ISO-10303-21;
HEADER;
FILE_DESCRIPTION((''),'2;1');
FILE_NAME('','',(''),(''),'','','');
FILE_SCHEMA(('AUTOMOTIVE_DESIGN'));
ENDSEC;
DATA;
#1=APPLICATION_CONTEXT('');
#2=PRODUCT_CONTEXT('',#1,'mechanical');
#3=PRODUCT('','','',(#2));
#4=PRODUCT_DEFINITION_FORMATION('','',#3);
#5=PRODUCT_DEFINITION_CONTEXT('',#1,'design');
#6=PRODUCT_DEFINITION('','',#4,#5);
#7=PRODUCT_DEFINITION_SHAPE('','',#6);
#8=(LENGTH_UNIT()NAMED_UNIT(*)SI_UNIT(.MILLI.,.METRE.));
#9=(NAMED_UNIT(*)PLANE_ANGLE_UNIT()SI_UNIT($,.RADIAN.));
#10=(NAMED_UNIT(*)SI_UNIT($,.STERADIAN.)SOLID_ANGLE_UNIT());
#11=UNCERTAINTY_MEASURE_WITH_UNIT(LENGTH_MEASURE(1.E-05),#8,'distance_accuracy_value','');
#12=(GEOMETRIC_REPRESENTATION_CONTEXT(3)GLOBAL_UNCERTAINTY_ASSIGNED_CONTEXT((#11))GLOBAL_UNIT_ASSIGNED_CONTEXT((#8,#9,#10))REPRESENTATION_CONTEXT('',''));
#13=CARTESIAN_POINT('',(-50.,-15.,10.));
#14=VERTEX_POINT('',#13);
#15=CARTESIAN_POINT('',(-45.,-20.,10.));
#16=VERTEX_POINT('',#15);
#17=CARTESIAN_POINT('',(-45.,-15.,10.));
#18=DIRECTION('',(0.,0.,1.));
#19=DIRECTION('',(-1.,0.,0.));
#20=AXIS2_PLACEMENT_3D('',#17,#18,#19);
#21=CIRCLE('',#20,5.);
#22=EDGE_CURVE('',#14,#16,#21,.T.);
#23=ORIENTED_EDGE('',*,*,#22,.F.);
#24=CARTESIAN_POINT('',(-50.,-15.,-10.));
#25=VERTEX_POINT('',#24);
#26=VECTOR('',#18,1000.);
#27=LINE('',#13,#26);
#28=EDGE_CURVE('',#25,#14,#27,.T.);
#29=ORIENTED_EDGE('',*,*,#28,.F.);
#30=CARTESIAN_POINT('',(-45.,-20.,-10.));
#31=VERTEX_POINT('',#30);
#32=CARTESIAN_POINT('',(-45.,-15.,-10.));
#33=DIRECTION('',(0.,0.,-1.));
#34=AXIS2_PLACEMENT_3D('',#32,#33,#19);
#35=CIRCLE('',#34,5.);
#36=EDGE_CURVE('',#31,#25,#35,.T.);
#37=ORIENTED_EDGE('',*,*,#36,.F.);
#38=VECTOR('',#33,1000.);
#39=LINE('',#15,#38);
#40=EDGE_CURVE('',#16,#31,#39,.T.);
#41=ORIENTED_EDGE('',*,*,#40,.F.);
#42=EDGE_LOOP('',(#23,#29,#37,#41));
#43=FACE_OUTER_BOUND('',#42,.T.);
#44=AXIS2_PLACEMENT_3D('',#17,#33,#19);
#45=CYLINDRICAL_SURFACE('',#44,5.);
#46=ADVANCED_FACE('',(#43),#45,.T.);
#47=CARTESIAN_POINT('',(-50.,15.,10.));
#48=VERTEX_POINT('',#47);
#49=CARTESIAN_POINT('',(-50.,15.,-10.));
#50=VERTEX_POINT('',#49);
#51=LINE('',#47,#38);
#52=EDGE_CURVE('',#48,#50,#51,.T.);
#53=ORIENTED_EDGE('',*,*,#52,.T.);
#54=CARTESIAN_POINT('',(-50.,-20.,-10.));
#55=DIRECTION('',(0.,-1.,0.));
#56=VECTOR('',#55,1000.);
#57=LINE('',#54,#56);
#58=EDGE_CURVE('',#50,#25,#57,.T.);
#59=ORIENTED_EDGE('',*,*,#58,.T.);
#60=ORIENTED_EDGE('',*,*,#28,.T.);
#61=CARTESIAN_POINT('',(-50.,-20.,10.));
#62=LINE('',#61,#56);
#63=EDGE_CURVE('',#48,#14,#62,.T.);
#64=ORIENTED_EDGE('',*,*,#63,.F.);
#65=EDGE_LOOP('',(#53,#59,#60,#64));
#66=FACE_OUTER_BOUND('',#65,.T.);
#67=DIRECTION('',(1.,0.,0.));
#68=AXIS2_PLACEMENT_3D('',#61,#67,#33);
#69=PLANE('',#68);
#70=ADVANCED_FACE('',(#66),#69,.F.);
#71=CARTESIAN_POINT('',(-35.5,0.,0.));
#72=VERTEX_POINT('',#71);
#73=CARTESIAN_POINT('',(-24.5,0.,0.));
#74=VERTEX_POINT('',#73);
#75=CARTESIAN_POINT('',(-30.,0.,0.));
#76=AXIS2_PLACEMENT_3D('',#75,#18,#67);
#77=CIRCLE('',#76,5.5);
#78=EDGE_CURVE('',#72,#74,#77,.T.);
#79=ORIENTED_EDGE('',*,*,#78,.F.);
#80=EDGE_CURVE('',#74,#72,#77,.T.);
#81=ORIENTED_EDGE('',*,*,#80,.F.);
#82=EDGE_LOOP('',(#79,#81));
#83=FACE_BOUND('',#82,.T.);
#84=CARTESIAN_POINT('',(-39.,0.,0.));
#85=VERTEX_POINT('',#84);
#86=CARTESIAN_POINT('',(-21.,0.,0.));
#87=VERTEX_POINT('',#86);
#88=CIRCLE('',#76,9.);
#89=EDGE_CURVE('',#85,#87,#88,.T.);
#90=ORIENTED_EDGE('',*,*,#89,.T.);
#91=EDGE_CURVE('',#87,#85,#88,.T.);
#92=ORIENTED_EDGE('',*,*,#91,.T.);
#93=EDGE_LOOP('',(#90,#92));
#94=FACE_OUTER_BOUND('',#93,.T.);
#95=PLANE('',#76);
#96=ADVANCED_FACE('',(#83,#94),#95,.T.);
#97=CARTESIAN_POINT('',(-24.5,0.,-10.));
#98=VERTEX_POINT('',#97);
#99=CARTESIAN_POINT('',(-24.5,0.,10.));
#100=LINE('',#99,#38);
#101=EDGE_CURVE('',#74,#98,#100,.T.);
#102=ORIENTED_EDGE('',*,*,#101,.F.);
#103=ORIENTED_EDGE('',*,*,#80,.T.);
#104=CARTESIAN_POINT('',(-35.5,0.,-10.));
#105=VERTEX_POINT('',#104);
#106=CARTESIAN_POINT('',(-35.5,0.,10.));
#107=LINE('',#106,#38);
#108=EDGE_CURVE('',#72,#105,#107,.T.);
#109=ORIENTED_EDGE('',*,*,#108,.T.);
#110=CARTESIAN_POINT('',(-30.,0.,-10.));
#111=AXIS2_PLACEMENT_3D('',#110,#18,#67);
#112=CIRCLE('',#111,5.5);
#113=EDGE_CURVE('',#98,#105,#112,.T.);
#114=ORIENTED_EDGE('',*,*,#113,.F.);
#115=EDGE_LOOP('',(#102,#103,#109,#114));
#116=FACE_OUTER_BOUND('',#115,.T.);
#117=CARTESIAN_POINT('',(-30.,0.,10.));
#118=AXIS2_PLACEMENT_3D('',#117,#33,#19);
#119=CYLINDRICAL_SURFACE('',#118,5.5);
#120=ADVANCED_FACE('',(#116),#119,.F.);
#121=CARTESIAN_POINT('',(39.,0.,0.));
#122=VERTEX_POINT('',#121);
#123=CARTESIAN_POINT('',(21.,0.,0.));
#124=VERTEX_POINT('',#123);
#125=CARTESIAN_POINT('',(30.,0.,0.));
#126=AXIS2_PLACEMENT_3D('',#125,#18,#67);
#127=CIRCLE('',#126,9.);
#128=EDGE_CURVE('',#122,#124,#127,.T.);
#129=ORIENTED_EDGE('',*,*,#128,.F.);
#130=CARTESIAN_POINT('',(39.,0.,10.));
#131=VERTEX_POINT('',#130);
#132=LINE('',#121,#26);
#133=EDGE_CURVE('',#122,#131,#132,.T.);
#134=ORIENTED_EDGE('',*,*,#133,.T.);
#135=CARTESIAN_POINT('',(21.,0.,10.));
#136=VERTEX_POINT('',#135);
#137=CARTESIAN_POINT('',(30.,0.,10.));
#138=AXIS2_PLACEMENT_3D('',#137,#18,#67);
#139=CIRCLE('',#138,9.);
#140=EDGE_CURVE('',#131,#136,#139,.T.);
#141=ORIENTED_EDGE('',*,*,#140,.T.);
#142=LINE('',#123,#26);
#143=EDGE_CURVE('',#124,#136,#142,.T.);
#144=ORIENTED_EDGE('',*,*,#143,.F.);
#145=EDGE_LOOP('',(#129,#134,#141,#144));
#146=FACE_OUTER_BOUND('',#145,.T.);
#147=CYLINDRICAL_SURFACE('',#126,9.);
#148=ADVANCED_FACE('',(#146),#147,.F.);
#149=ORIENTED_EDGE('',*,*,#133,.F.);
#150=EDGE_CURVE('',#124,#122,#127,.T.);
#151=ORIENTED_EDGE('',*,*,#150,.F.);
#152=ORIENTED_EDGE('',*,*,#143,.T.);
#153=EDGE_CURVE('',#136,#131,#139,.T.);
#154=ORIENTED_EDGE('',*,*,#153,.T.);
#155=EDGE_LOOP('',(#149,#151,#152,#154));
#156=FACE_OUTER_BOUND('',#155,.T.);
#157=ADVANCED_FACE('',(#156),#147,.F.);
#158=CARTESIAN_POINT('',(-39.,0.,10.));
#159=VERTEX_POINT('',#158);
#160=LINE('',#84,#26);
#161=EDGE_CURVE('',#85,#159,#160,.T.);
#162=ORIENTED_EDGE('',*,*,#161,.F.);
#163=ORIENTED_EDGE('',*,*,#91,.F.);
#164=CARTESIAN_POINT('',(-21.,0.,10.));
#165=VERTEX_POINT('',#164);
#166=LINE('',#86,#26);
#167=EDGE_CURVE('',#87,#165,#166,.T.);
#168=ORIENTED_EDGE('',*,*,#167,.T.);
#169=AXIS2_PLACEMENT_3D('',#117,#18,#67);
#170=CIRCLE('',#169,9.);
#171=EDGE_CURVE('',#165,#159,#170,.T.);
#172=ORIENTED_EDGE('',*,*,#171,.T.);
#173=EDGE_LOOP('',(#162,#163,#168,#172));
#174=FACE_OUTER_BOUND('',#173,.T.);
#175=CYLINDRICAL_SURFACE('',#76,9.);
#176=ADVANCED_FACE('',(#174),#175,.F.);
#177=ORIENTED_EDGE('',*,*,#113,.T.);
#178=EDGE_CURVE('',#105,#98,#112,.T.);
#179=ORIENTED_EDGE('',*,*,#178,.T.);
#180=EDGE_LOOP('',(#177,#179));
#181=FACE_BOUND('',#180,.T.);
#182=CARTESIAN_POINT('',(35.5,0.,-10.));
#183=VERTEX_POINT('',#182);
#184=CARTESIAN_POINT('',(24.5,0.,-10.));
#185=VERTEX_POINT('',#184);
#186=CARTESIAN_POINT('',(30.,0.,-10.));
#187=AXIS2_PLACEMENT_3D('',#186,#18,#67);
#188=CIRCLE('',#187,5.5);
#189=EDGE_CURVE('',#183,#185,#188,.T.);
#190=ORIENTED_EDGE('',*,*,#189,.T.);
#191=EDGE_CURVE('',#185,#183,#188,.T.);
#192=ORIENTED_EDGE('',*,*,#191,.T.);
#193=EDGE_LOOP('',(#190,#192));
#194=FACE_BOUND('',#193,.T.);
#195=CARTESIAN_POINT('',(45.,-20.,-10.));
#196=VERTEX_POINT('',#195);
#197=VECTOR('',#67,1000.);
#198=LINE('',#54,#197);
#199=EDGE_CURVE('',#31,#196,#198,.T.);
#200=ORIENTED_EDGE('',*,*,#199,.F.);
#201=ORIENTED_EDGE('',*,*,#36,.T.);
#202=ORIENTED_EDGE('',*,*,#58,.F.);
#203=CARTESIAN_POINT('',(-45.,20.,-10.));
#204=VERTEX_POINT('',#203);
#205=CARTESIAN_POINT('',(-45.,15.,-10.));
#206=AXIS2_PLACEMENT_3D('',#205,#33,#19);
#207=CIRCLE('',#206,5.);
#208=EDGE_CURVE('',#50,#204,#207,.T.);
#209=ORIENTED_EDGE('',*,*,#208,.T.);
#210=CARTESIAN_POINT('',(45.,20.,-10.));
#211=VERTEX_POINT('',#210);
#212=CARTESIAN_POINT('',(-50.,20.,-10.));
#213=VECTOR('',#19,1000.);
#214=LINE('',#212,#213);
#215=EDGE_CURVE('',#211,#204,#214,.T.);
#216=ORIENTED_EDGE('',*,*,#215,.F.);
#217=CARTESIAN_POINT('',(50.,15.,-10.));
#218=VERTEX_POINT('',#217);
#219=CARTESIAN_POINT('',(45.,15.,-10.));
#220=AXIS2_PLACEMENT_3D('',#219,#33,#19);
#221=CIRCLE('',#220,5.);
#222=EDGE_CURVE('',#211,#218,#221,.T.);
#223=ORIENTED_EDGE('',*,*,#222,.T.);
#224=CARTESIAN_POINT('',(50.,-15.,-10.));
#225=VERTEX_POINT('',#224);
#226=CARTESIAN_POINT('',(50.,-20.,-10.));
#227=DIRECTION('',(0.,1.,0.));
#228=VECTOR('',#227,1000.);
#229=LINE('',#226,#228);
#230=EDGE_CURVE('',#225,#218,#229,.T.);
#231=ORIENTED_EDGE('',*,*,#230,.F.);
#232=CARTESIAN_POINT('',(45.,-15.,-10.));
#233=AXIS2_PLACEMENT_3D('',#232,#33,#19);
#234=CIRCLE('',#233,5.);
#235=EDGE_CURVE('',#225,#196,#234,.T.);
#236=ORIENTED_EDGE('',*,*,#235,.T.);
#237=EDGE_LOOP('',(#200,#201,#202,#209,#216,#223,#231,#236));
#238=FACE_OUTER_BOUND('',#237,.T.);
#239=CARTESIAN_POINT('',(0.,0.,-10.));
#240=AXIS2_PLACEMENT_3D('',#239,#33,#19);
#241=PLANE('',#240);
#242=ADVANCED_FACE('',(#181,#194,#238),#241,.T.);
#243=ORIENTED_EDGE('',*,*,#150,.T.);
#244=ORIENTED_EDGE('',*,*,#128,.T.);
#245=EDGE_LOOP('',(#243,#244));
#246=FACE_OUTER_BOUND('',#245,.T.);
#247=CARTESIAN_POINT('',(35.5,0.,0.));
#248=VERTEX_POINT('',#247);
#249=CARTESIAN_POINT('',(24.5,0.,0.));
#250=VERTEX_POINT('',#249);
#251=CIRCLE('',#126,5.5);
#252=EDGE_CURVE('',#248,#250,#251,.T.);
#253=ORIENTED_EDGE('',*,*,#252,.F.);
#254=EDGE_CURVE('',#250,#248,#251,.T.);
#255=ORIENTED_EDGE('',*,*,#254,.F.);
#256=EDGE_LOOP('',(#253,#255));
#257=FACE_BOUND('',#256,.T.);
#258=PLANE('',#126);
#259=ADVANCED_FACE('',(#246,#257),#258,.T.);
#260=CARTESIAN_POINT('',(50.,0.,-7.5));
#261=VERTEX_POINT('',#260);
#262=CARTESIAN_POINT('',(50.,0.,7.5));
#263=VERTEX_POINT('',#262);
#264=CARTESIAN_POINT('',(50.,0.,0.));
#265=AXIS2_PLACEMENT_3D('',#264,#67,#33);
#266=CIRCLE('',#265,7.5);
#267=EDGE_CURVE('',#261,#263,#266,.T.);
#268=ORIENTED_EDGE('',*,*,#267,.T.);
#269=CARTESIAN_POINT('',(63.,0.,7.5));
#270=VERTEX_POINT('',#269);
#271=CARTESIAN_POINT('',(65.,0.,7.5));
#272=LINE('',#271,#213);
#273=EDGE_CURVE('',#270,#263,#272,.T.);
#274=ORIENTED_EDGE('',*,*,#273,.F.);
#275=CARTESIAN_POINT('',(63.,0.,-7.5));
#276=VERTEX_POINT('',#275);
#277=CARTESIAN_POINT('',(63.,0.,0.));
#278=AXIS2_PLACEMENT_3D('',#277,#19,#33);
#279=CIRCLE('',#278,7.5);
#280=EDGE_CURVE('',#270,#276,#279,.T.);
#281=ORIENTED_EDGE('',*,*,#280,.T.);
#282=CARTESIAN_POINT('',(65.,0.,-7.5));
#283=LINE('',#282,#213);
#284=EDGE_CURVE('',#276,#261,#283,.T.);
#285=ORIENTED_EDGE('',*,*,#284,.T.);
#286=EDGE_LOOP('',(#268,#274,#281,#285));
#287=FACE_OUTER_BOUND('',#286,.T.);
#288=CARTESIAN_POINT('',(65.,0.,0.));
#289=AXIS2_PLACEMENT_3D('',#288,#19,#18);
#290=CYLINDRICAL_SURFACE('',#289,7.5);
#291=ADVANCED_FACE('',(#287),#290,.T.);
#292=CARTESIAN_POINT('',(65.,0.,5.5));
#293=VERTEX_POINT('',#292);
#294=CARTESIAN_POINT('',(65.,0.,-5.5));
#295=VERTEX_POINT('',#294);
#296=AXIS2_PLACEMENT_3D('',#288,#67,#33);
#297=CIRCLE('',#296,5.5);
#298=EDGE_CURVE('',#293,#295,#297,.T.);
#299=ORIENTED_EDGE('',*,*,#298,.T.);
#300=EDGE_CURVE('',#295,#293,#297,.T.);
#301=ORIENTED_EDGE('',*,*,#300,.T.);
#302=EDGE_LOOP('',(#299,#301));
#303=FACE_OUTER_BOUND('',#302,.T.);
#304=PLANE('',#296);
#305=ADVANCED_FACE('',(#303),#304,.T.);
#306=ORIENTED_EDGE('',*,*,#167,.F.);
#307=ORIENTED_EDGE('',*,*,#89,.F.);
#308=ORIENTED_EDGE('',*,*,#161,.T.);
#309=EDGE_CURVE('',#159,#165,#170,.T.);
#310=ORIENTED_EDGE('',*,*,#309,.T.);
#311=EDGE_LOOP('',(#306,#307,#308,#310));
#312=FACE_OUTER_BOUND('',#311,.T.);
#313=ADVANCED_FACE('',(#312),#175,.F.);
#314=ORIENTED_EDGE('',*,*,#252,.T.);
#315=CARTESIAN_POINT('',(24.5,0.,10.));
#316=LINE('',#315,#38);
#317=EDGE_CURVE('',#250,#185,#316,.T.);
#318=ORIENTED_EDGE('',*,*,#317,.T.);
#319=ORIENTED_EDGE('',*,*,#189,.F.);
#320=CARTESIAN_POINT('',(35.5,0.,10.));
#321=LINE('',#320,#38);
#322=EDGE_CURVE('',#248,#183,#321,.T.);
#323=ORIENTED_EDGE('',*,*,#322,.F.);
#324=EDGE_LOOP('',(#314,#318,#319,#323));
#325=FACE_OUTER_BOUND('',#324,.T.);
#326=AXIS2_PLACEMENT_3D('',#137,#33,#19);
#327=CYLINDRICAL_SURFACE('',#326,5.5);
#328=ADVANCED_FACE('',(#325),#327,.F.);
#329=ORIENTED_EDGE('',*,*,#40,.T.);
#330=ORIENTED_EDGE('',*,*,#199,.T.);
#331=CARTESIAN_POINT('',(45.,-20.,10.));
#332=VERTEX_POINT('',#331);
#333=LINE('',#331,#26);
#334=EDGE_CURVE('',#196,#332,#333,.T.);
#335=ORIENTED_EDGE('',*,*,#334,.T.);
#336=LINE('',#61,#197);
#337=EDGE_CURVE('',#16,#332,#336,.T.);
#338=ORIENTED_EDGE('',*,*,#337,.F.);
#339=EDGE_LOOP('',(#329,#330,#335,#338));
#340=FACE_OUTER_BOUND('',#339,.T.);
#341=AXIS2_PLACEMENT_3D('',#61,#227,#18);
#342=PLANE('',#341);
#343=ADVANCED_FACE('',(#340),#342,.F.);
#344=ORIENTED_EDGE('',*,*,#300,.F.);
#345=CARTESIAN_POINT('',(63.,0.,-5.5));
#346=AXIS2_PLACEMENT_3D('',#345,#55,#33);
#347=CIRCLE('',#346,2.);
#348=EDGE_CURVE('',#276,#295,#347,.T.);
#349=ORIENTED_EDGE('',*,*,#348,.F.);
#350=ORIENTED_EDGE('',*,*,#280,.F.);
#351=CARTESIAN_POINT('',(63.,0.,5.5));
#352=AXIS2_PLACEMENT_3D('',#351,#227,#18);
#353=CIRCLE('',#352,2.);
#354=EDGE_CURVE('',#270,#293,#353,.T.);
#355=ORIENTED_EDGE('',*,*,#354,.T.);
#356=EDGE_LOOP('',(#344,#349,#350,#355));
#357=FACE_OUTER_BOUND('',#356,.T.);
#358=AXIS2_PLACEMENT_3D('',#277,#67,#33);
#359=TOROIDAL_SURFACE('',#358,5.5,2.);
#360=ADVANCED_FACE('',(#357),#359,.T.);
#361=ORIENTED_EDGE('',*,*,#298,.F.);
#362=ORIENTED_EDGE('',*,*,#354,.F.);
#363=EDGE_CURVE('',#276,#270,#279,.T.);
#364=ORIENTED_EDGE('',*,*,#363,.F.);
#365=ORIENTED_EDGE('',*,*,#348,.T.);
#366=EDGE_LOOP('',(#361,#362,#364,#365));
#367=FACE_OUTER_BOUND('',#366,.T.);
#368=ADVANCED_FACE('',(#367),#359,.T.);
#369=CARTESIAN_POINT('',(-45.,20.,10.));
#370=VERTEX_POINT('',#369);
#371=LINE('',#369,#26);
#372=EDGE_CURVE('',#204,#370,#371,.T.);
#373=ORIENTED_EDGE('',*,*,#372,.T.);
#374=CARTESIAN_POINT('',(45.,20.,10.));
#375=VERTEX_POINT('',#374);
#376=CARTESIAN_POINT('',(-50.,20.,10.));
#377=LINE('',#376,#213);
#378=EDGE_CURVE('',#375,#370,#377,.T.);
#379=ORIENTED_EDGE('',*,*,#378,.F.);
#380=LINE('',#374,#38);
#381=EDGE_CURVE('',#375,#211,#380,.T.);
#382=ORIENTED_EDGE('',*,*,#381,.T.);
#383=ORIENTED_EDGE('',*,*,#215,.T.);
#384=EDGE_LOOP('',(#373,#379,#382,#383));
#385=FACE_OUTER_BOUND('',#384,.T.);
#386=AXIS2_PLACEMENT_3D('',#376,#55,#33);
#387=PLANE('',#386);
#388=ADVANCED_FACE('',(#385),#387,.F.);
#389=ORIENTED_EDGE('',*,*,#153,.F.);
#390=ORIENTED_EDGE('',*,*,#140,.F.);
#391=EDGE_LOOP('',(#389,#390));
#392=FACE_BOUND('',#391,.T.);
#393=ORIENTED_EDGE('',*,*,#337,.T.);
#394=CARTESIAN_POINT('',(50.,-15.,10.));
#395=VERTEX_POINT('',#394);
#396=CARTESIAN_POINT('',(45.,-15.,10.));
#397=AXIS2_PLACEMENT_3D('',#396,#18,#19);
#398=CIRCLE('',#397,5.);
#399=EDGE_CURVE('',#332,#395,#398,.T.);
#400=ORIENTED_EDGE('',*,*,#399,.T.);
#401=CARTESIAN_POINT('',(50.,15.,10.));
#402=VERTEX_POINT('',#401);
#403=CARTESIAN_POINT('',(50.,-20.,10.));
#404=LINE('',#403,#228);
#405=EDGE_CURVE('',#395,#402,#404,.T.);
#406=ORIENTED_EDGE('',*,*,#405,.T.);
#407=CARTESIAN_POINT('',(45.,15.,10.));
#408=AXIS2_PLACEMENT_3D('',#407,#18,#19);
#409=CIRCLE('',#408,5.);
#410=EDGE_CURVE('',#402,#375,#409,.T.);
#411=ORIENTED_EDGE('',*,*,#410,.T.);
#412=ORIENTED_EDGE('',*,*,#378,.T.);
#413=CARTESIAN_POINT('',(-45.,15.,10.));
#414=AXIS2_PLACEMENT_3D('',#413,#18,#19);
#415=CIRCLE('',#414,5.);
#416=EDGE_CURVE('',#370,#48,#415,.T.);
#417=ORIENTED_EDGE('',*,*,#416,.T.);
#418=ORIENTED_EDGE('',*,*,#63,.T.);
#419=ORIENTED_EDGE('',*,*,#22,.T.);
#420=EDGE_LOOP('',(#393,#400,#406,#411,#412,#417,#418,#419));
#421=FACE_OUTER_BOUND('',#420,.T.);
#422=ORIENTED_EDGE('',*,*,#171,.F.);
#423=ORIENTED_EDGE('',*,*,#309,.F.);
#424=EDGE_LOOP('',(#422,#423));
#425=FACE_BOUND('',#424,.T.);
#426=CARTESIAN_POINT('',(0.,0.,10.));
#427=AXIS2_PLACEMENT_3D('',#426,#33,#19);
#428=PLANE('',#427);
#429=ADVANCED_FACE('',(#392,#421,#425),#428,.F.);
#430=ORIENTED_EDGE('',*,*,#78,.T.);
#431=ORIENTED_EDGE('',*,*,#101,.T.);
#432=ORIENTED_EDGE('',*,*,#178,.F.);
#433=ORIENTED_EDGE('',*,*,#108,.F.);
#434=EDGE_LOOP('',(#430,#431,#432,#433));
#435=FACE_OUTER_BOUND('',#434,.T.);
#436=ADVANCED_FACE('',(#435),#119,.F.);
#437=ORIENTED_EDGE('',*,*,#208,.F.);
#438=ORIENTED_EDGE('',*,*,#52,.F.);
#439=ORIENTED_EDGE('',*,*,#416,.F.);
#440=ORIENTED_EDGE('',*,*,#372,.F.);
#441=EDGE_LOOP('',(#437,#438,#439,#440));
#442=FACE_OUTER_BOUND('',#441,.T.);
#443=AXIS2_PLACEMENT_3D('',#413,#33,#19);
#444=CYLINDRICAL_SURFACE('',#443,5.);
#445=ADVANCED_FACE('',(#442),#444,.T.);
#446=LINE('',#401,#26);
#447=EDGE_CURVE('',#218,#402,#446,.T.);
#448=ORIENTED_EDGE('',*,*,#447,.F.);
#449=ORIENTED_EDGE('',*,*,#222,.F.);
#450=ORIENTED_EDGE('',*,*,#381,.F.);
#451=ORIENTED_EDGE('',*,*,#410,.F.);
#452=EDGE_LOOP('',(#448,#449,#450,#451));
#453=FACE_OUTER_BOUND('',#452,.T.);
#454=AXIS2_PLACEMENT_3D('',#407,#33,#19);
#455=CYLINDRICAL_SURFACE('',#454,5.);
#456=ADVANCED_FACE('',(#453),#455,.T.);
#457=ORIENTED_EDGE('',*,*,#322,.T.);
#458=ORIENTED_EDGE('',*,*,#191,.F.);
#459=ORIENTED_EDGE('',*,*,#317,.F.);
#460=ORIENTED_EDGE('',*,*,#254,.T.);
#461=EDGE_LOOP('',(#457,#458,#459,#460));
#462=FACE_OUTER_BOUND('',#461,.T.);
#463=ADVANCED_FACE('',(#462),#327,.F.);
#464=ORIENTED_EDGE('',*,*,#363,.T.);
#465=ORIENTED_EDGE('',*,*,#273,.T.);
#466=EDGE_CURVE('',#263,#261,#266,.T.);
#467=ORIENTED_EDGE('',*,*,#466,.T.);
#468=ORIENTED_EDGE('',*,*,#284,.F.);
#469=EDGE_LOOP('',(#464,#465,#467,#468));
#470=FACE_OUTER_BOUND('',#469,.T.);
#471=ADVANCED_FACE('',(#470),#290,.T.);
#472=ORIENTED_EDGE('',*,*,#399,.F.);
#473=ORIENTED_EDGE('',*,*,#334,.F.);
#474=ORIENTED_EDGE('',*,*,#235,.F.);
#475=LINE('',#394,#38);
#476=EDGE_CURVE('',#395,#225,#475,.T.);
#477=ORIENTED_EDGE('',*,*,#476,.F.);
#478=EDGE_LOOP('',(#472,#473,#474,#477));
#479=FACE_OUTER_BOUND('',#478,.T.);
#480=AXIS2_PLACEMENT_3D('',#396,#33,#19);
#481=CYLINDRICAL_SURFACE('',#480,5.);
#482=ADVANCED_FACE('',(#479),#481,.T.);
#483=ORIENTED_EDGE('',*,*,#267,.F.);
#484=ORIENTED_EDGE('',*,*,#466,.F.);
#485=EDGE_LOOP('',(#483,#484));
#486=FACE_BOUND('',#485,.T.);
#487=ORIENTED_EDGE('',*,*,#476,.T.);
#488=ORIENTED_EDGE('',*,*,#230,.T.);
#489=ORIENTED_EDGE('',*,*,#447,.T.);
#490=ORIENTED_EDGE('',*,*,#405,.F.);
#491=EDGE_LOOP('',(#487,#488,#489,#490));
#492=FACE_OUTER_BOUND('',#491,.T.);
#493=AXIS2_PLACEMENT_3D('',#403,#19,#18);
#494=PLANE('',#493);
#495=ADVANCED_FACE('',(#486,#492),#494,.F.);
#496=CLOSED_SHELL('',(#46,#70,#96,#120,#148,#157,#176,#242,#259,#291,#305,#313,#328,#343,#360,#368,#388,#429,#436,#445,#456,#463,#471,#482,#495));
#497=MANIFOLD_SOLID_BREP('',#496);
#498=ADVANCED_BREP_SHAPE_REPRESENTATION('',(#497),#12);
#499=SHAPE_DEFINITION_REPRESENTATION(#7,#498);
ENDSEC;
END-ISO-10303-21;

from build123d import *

# Parameters (mm, degrees)
SKETCH1_W           = 100
SKETCH1_H           = 40
SKETCH1_R           = 5.5
BOSS_EXTRUDE1_DEPTH = 10
SKETCH2_R           = 7.5
BOSS_EXTRUDE2_DEPTH = 15
FILLET1_R           = 2
SKETCH3_R           = 9
CUT_EXTRUDE1_DEPTH  = 10
FILLET2_R           = 5


with BuildPart() as part:
    # Sketch1 → Boss-Extrude1 (new, symmetric)
    with BuildSketch(Plane.XY):
        Rectangle(SKETCH1_W, SKETCH1_H)
        with Locations((-30, 0)):
            Circle(SKETCH1_R, mode=Mode.SUBTRACT)
        with Locations((30, 0)):
            Circle(SKETCH1_R, mode=Mode.SUBTRACT)
    extrude(amount=BOSS_EXTRUDE1_DEPTH, both=True)

    # Sketch2 → Boss-Extrude2 (add)
    with BuildSketch(Plane(origin=(50, 0, 0), x_dir=(0, 0, -1), z_dir=(1, 0, 0))):
        Circle(SKETCH2_R)
    extrude(amount=BOSS_EXTRUDE2_DEPTH)

    # Fillet1
    fillet1_edges = [part.edges().sort_by_distance(p)[0] for p in [
        (65, 0, 7.5),
    ]]
    fillet(fillet1_edges, radius=FILLET1_R)

    # Sketch3 → Cut-Extrude1 (cut)
    with BuildSketch(Plane.XY.offset(10)):
        with Locations((-30, 0)):
            Circle(SKETCH3_R)
        with Locations((30, 0)):
            Circle(SKETCH3_R)
    extrude(amount=-CUT_EXTRUDE1_DEPTH, mode=Mode.SUBTRACT)

    # Fillet2
    fillet2_edges = [part.edges().sort_by_distance(p)[0] for p in [
        (50, -20, 0),
        (-50, -20, 0),
        (-50, 20, 0),
        (50, 20, 0),
    ]]
    fillet(fillet2_edges, radius=FILLET2_R)


solid = part.part
